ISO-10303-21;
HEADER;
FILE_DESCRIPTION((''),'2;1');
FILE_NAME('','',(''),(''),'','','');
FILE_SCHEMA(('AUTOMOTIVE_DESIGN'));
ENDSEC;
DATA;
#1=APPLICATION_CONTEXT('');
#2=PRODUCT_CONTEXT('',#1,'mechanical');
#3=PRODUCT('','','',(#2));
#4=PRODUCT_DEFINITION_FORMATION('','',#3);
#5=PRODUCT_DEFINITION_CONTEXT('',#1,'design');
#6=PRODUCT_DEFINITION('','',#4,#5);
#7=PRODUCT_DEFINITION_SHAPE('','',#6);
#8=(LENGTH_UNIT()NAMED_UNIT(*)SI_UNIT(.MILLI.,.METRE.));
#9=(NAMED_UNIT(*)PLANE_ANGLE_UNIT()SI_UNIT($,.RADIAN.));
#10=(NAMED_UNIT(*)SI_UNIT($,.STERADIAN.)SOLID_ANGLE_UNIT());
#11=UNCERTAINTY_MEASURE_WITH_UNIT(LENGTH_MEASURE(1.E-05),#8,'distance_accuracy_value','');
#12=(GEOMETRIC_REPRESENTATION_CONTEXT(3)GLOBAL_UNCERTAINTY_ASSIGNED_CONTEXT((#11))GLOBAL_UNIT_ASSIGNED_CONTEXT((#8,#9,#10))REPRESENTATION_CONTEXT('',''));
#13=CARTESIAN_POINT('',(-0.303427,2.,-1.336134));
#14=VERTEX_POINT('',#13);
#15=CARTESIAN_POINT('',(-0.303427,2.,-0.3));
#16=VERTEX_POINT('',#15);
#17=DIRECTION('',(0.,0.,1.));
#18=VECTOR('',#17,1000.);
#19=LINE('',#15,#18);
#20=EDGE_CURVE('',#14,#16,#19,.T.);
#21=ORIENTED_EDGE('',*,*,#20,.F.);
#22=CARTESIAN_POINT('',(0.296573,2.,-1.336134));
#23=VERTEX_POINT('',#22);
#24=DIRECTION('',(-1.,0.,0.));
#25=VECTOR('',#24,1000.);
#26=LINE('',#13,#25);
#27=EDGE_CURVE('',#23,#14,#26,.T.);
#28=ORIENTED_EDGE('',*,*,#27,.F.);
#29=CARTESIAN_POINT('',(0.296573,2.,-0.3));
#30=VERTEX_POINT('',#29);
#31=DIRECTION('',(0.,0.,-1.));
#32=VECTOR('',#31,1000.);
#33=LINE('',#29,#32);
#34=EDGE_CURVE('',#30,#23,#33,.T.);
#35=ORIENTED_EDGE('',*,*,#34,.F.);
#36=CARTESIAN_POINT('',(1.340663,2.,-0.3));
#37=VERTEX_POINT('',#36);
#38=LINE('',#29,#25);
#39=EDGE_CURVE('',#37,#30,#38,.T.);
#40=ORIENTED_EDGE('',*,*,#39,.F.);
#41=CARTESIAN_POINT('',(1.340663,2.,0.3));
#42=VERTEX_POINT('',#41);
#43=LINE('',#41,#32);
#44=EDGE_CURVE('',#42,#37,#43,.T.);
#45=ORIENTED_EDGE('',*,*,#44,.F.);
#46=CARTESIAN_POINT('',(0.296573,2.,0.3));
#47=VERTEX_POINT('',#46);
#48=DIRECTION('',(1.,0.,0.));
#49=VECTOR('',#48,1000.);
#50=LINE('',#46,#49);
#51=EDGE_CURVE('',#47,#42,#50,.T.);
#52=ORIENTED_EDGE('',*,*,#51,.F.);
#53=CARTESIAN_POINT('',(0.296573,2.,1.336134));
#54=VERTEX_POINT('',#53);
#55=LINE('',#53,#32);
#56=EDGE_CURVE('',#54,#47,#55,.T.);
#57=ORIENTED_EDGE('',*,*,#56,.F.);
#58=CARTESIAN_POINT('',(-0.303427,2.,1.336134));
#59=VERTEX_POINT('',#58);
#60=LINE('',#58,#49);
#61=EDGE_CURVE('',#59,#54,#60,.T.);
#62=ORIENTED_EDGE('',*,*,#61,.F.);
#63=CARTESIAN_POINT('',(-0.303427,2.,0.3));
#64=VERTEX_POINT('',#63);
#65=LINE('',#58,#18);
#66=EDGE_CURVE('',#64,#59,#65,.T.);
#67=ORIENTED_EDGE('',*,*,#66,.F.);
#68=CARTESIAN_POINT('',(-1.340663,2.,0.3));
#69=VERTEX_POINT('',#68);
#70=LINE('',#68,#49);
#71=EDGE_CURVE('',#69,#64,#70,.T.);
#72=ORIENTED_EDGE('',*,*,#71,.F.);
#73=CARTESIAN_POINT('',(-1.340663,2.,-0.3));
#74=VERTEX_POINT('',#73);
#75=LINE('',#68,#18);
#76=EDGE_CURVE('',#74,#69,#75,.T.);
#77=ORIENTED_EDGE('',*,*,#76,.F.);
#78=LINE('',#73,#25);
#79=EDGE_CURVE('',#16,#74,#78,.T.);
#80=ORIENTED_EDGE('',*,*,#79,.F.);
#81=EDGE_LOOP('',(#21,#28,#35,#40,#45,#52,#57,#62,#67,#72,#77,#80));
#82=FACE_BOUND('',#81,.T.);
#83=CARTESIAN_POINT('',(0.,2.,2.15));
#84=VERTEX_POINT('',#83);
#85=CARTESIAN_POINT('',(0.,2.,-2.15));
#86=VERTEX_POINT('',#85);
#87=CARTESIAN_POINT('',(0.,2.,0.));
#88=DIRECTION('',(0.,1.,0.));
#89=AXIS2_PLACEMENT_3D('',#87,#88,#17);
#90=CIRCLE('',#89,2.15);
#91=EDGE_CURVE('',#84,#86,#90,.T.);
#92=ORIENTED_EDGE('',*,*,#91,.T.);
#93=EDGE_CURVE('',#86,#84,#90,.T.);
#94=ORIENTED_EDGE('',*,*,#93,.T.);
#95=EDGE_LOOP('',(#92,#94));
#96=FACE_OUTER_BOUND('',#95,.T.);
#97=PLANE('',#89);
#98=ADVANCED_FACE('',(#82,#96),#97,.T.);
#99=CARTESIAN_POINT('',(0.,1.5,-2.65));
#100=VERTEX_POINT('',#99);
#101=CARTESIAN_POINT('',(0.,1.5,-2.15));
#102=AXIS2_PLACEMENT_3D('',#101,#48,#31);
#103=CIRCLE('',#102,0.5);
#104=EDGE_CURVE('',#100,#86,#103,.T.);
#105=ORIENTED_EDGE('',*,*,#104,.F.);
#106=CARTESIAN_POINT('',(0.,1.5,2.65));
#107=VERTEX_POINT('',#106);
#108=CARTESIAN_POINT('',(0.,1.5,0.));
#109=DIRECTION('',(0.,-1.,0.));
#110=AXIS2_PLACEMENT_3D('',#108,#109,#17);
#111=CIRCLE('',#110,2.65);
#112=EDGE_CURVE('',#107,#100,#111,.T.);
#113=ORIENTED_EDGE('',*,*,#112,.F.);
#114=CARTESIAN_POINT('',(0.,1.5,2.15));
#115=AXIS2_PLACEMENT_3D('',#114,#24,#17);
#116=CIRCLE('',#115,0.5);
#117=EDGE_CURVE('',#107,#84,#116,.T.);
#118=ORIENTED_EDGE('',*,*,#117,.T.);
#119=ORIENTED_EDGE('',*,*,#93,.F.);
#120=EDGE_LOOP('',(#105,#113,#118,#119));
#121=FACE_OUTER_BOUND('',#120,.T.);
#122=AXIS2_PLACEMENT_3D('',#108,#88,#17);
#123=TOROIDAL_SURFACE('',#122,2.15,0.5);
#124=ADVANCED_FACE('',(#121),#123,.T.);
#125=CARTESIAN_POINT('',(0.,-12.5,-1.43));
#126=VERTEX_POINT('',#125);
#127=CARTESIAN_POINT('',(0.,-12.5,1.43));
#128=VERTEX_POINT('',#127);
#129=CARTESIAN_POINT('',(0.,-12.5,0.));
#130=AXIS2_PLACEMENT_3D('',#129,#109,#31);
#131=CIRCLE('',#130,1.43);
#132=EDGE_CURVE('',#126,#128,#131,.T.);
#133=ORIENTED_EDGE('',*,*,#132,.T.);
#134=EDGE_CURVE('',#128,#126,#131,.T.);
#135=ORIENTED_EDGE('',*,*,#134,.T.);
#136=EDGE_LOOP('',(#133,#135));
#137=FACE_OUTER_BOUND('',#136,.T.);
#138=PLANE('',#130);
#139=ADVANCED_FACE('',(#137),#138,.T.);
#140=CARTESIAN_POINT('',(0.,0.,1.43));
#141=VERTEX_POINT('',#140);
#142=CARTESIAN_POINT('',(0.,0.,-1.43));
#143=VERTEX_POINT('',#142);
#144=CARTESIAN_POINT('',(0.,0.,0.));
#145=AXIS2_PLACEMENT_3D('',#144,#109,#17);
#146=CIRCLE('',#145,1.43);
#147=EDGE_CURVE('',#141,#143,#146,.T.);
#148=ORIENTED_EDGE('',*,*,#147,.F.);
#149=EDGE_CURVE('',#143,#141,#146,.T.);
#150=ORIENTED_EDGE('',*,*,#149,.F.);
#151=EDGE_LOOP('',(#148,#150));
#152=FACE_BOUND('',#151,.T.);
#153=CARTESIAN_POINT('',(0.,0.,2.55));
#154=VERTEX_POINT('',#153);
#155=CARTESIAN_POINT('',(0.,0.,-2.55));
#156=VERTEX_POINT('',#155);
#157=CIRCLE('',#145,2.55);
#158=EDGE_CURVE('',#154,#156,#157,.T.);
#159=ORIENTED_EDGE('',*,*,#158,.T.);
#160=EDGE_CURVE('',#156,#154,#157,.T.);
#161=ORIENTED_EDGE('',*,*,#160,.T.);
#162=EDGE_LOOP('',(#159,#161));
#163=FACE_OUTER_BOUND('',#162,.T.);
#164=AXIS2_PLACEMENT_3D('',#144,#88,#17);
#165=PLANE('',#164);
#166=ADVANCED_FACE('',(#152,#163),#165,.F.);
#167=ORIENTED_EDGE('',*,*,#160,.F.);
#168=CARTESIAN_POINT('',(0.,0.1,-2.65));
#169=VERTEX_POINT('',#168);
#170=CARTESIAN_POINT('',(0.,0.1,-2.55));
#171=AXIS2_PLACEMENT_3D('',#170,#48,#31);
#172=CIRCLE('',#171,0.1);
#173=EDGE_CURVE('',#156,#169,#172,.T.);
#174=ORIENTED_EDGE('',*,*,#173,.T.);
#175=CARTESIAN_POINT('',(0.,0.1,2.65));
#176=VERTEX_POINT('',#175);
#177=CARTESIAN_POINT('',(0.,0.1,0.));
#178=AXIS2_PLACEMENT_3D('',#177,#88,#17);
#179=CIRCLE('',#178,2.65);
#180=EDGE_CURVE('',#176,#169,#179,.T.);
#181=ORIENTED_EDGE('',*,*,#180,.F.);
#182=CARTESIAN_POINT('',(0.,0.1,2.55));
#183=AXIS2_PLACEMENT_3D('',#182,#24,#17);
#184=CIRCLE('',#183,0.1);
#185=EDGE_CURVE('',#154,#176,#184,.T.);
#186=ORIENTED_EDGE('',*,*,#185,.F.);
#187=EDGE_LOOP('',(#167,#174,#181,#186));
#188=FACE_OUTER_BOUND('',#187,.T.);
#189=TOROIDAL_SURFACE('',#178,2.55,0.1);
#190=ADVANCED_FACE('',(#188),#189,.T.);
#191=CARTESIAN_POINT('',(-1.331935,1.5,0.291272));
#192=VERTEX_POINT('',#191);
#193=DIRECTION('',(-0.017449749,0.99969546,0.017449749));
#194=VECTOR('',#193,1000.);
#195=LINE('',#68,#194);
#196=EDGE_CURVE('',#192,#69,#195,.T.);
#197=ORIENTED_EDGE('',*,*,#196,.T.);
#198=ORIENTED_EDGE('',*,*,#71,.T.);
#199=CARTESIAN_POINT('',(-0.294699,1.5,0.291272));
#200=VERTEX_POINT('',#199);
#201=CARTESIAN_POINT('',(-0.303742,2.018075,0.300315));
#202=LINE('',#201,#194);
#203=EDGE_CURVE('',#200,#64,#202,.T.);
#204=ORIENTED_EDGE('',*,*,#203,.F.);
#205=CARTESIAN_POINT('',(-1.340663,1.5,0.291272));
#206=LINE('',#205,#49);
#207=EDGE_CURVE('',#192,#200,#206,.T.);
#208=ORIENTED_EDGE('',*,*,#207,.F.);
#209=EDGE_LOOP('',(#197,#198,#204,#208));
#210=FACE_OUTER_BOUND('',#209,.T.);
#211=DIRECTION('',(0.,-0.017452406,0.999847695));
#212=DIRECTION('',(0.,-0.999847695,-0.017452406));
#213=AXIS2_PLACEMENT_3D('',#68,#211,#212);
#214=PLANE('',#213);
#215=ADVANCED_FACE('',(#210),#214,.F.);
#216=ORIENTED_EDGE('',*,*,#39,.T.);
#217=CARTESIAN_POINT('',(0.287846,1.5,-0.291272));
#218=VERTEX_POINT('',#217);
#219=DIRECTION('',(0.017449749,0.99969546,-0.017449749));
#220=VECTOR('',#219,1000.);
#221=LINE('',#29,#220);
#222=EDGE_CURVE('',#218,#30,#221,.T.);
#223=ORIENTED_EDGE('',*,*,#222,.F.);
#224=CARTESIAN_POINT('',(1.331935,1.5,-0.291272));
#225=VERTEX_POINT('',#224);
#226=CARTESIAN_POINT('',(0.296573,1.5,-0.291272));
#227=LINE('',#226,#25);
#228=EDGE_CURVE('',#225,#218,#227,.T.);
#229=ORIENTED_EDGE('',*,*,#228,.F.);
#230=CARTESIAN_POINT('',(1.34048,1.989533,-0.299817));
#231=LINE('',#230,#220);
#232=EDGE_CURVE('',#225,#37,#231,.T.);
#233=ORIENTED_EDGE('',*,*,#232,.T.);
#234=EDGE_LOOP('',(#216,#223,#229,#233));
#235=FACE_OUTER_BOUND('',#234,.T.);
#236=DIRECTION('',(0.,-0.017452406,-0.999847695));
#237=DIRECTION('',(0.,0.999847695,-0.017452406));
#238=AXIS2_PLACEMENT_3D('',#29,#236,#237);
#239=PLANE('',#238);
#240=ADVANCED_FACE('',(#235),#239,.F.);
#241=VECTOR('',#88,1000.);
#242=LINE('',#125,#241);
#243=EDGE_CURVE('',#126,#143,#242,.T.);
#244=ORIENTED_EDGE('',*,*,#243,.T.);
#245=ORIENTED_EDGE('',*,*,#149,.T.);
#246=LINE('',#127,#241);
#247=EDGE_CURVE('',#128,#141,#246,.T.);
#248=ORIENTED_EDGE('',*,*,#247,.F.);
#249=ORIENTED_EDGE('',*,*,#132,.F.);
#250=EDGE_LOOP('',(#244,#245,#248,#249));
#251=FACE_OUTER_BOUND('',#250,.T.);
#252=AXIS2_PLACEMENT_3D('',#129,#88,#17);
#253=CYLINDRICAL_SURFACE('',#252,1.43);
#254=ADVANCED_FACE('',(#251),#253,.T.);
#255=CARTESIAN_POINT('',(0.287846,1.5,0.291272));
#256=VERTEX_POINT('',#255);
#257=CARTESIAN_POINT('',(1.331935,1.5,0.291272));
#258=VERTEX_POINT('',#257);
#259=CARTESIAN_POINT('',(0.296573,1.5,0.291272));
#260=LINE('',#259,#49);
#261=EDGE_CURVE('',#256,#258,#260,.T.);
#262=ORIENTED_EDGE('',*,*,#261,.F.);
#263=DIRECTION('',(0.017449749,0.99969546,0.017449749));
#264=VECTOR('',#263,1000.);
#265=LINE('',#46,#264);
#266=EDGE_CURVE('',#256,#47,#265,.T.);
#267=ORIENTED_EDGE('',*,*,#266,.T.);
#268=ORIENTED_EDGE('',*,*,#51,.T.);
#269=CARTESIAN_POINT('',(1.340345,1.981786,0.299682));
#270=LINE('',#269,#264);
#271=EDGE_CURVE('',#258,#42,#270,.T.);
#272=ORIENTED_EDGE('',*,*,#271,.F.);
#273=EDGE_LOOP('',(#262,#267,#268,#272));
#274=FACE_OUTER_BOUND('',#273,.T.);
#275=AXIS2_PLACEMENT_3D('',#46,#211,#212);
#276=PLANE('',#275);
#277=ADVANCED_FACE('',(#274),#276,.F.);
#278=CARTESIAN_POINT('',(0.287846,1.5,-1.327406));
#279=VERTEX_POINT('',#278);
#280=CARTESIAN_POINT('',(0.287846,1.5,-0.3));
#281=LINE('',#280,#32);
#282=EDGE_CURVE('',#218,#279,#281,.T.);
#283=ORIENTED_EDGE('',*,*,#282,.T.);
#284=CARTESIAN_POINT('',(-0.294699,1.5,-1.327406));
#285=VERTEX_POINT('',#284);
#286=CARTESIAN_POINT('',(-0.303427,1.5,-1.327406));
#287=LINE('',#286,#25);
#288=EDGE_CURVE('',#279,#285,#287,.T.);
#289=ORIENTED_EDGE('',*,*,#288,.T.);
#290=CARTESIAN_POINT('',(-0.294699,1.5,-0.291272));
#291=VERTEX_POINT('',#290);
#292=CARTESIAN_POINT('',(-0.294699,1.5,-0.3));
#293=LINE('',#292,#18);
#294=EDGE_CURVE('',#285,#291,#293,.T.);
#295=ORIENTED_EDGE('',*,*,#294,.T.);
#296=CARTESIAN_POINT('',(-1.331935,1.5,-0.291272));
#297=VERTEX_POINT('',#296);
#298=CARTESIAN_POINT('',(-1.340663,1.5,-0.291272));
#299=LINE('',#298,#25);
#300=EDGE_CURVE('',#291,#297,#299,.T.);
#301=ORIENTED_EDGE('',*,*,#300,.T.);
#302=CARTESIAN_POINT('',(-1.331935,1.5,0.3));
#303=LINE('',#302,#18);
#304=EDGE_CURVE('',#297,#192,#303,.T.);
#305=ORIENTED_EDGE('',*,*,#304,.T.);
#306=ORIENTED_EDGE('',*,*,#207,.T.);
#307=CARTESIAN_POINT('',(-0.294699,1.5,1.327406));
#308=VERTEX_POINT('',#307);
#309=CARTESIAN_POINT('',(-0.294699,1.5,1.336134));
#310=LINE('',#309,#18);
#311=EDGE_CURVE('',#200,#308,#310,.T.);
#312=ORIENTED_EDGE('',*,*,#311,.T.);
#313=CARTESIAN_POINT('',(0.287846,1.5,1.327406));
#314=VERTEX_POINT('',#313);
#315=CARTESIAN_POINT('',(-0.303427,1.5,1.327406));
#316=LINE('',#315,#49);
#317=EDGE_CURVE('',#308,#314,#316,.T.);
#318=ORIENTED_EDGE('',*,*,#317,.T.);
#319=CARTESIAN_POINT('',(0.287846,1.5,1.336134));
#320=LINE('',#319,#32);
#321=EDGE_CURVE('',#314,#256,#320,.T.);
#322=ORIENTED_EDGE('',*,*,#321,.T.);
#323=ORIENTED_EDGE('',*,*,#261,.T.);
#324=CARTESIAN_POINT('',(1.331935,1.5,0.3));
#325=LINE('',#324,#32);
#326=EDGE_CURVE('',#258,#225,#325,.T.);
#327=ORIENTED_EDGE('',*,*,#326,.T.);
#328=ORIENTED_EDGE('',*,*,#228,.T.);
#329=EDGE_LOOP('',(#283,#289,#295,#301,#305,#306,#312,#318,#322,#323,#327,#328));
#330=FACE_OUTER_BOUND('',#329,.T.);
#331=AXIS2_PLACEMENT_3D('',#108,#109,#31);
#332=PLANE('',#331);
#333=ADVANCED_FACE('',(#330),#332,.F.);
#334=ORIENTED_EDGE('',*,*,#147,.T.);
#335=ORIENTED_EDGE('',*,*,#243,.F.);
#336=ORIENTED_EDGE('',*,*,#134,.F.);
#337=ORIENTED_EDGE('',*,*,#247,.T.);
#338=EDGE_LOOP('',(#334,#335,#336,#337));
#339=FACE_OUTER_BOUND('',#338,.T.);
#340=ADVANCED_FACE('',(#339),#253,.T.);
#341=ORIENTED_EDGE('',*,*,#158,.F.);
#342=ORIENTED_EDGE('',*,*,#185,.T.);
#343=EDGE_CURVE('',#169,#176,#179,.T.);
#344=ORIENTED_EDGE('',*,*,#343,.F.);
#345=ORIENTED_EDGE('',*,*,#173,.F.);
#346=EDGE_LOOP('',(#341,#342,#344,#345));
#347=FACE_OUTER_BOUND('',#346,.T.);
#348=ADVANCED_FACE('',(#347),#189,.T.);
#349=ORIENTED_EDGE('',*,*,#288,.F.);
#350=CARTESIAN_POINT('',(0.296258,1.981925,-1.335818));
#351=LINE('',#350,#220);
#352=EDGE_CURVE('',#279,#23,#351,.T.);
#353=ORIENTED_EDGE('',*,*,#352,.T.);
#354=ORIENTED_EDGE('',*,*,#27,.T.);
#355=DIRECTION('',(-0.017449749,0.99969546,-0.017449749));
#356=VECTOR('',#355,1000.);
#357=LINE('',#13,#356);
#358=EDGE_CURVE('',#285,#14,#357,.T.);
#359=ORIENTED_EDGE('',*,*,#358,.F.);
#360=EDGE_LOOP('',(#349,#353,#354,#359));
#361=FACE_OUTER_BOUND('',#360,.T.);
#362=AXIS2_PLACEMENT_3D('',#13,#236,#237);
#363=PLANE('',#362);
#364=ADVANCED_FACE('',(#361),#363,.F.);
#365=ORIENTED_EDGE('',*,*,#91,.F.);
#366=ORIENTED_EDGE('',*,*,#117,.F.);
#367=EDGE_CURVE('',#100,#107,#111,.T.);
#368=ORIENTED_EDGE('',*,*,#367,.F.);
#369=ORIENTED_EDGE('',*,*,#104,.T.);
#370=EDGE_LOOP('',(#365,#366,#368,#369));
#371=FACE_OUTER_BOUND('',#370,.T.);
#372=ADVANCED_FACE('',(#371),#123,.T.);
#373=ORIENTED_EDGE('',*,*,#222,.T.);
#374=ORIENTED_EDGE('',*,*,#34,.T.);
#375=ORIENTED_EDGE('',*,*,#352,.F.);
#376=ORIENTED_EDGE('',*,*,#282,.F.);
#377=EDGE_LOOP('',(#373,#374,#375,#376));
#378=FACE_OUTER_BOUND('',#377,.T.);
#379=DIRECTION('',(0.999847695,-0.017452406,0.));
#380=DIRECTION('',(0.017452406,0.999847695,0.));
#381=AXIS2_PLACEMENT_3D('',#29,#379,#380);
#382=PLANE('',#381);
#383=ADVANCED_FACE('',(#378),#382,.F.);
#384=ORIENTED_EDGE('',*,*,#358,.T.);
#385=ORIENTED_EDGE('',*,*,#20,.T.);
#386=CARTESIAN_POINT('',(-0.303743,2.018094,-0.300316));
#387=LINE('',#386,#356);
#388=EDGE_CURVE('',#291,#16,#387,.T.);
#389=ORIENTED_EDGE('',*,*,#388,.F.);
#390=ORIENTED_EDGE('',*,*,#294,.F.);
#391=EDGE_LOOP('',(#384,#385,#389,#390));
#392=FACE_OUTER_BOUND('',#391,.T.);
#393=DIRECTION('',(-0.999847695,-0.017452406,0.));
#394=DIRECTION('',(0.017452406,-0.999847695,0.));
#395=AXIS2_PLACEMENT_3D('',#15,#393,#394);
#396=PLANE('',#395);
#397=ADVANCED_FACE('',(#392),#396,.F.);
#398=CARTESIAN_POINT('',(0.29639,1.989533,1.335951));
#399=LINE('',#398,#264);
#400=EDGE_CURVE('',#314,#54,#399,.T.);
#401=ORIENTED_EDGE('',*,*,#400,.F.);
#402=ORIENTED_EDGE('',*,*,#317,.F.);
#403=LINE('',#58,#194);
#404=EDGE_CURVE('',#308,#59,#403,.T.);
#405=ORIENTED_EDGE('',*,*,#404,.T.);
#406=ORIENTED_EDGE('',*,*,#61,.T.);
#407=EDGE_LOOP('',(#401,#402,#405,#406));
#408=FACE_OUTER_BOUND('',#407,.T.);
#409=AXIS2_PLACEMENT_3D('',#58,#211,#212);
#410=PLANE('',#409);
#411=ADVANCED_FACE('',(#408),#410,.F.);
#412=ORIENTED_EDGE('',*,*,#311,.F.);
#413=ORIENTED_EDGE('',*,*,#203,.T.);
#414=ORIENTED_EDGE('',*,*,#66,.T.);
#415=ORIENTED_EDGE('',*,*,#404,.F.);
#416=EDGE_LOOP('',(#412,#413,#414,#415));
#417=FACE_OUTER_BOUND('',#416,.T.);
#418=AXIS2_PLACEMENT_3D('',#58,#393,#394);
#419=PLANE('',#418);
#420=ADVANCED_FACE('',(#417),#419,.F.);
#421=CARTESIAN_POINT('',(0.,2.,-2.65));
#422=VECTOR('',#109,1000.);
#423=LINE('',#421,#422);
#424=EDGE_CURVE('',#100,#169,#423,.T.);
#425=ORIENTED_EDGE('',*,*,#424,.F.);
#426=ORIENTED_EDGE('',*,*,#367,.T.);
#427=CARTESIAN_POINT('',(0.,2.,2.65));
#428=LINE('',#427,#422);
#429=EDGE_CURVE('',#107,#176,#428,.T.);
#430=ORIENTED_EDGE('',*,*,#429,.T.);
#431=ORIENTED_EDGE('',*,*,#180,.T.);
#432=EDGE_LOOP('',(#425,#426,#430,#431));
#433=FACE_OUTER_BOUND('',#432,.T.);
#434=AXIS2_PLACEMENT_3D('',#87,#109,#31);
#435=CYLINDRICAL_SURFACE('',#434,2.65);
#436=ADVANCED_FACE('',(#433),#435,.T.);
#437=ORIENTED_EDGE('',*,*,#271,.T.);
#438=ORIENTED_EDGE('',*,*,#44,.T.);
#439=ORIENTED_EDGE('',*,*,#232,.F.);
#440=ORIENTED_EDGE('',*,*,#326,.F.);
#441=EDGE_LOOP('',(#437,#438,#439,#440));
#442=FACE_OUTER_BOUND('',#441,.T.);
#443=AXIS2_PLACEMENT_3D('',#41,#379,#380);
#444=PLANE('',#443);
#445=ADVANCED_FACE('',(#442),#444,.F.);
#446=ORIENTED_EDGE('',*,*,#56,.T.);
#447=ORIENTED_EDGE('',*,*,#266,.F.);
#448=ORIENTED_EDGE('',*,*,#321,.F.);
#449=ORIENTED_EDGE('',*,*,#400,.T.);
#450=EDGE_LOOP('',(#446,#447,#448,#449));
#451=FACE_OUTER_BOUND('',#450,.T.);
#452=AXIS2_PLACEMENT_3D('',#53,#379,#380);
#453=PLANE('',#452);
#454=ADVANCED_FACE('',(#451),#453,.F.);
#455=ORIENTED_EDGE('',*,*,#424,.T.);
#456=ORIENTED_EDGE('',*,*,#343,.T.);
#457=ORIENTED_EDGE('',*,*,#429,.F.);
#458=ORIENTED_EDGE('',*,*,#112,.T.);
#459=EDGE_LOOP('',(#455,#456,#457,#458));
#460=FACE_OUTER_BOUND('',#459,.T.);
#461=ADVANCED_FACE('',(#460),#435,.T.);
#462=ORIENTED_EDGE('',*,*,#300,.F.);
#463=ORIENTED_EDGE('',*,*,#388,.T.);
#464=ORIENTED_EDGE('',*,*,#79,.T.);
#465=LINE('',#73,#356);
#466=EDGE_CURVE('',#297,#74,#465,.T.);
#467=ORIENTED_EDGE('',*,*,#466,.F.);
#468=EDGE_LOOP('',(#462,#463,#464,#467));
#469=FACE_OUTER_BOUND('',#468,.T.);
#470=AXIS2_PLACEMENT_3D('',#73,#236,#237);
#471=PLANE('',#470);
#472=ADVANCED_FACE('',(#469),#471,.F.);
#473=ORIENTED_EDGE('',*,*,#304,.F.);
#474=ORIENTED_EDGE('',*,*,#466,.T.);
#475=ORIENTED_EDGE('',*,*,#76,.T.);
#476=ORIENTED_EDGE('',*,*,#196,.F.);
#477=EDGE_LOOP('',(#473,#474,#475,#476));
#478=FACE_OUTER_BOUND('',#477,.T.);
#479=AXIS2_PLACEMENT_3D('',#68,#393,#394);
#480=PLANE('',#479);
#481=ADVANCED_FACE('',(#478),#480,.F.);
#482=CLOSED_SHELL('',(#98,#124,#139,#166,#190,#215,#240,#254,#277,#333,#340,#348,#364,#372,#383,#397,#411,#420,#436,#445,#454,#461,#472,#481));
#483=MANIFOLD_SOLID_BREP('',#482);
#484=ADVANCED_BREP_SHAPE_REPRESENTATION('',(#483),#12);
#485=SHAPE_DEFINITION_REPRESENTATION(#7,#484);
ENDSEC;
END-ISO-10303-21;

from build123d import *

# Parameters (mm, degrees)
SKETCH1_R           = 2.65
BOSS_EXTRUDE1_DEPTH = 2
SKETCH2_R           = 1.43
BOSS_EXTRUDE2_DEPTH = 12.5
FILLET1_R           = 0.5
FILLET2_R           = 0.1
CUT_EXTRUDE1_DEPTH  = 0.5
CUT_EXTRUDE1_DRAFT  = -1


with BuildPart() as part:
    # Sketch1 → Boss-Extrude1 (new body)
    with BuildSketch(Plane(origin=(0, 0, 0), x_dir=(1, 0, 0), z_dir=(0, 1, 0))):
        with Locations(Location((0, 0, 0), (0, 0, 270))):
            Circle(SKETCH1_R)
    extrude(amount=BOSS_EXTRUDE1_DEPTH)

    # Sketch2 → Boss-Extrude2 (add)
    with BuildSketch(Plane.XZ):
        with Locations(Location((0, 0, 0), (0, 0, 90))):
            Circle(SKETCH2_R)
    extrude(amount=BOSS_EXTRUDE2_DEPTH)

    # Fillet1
    fillet1_edges = [part.edges().sort_by_distance(p)[0] for p in [
        (0, 2, -2.65),
    ]]
    fillet(fillet1_edges, radius=FILLET1_R)

    # Fillet2
    fillet2_edges = [part.edges().sort_by_distance(p)[0] for p in [
        (0, 0, -2.65),
    ]]
    fillet(fillet2_edges, radius=FILLET2_R)


with BuildPart() as cut_extrude1_tool:
    # Sketch3 → Cut-Extrude1 (with draft: the straight prism first)
    with BuildSketch(Plane(origin=(0, 2, 0), x_dir=(1, 0, 0), z_dir=(0, 1, 0))):
        Polygon((0.296573117, 0.3), (0.296573117, 1.336133674), (-0.303426883, 1.336133674), (-0.303426883, 0.3), (-1.340662941, 0.3), (-1.340662941, -0.3), (-0.303426883, -0.3), (-0.303426883, -1.336133674), (0.296573117, -1.336133674), (0.296573117, -0.3), (1.340662941, -0.3), (1.340662941, 0.3), align=None)
    extrude(amount=-CUT_EXTRUDE1_DEPTH)
    # Cut-Extrude1: the draft: its side faces are tilted about the plane it starts from
    cut_extrude1_sides = [cut_extrude1_tool.faces().sort_by_distance(p)[0] for p in [
        (0.296573117, 1.75, -0.818066837),
        (-0.003426883, 1.75, -1.336133674),
        (-0.303426883, 1.75, -0.818066837),
        (-0.822044912, 1.75, -0.3),
        (-1.340662941, 1.75, 0),
        (-0.822044912, 1.75, 0.3),
        (-0.303426883, 1.75, 0.818066837),
        (-0.003426883, 1.75, 1.336133674),
        (0.296573117, 1.75, 0.818066837),
        (0.818618029, 1.75, 0.3),
        (1.340662941, 1.75, 0),
        (0.818618029, 1.75, -0.3),
    ]]
    draft(cut_extrude1_sides, Plane(origin=(0, 2, 0), x_dir=(1, 0, 0), z_dir=(0, 1, 0)), CUT_EXTRUDE1_DRAFT)


with BuildPart() as part_1:
    add(part.part)

    # Cut-Extrude1: cut by cut_extrude1_tool
    add(cut_extrude1_tool.part, mode=Mode.SUBTRACT)


solid = part_1.part
